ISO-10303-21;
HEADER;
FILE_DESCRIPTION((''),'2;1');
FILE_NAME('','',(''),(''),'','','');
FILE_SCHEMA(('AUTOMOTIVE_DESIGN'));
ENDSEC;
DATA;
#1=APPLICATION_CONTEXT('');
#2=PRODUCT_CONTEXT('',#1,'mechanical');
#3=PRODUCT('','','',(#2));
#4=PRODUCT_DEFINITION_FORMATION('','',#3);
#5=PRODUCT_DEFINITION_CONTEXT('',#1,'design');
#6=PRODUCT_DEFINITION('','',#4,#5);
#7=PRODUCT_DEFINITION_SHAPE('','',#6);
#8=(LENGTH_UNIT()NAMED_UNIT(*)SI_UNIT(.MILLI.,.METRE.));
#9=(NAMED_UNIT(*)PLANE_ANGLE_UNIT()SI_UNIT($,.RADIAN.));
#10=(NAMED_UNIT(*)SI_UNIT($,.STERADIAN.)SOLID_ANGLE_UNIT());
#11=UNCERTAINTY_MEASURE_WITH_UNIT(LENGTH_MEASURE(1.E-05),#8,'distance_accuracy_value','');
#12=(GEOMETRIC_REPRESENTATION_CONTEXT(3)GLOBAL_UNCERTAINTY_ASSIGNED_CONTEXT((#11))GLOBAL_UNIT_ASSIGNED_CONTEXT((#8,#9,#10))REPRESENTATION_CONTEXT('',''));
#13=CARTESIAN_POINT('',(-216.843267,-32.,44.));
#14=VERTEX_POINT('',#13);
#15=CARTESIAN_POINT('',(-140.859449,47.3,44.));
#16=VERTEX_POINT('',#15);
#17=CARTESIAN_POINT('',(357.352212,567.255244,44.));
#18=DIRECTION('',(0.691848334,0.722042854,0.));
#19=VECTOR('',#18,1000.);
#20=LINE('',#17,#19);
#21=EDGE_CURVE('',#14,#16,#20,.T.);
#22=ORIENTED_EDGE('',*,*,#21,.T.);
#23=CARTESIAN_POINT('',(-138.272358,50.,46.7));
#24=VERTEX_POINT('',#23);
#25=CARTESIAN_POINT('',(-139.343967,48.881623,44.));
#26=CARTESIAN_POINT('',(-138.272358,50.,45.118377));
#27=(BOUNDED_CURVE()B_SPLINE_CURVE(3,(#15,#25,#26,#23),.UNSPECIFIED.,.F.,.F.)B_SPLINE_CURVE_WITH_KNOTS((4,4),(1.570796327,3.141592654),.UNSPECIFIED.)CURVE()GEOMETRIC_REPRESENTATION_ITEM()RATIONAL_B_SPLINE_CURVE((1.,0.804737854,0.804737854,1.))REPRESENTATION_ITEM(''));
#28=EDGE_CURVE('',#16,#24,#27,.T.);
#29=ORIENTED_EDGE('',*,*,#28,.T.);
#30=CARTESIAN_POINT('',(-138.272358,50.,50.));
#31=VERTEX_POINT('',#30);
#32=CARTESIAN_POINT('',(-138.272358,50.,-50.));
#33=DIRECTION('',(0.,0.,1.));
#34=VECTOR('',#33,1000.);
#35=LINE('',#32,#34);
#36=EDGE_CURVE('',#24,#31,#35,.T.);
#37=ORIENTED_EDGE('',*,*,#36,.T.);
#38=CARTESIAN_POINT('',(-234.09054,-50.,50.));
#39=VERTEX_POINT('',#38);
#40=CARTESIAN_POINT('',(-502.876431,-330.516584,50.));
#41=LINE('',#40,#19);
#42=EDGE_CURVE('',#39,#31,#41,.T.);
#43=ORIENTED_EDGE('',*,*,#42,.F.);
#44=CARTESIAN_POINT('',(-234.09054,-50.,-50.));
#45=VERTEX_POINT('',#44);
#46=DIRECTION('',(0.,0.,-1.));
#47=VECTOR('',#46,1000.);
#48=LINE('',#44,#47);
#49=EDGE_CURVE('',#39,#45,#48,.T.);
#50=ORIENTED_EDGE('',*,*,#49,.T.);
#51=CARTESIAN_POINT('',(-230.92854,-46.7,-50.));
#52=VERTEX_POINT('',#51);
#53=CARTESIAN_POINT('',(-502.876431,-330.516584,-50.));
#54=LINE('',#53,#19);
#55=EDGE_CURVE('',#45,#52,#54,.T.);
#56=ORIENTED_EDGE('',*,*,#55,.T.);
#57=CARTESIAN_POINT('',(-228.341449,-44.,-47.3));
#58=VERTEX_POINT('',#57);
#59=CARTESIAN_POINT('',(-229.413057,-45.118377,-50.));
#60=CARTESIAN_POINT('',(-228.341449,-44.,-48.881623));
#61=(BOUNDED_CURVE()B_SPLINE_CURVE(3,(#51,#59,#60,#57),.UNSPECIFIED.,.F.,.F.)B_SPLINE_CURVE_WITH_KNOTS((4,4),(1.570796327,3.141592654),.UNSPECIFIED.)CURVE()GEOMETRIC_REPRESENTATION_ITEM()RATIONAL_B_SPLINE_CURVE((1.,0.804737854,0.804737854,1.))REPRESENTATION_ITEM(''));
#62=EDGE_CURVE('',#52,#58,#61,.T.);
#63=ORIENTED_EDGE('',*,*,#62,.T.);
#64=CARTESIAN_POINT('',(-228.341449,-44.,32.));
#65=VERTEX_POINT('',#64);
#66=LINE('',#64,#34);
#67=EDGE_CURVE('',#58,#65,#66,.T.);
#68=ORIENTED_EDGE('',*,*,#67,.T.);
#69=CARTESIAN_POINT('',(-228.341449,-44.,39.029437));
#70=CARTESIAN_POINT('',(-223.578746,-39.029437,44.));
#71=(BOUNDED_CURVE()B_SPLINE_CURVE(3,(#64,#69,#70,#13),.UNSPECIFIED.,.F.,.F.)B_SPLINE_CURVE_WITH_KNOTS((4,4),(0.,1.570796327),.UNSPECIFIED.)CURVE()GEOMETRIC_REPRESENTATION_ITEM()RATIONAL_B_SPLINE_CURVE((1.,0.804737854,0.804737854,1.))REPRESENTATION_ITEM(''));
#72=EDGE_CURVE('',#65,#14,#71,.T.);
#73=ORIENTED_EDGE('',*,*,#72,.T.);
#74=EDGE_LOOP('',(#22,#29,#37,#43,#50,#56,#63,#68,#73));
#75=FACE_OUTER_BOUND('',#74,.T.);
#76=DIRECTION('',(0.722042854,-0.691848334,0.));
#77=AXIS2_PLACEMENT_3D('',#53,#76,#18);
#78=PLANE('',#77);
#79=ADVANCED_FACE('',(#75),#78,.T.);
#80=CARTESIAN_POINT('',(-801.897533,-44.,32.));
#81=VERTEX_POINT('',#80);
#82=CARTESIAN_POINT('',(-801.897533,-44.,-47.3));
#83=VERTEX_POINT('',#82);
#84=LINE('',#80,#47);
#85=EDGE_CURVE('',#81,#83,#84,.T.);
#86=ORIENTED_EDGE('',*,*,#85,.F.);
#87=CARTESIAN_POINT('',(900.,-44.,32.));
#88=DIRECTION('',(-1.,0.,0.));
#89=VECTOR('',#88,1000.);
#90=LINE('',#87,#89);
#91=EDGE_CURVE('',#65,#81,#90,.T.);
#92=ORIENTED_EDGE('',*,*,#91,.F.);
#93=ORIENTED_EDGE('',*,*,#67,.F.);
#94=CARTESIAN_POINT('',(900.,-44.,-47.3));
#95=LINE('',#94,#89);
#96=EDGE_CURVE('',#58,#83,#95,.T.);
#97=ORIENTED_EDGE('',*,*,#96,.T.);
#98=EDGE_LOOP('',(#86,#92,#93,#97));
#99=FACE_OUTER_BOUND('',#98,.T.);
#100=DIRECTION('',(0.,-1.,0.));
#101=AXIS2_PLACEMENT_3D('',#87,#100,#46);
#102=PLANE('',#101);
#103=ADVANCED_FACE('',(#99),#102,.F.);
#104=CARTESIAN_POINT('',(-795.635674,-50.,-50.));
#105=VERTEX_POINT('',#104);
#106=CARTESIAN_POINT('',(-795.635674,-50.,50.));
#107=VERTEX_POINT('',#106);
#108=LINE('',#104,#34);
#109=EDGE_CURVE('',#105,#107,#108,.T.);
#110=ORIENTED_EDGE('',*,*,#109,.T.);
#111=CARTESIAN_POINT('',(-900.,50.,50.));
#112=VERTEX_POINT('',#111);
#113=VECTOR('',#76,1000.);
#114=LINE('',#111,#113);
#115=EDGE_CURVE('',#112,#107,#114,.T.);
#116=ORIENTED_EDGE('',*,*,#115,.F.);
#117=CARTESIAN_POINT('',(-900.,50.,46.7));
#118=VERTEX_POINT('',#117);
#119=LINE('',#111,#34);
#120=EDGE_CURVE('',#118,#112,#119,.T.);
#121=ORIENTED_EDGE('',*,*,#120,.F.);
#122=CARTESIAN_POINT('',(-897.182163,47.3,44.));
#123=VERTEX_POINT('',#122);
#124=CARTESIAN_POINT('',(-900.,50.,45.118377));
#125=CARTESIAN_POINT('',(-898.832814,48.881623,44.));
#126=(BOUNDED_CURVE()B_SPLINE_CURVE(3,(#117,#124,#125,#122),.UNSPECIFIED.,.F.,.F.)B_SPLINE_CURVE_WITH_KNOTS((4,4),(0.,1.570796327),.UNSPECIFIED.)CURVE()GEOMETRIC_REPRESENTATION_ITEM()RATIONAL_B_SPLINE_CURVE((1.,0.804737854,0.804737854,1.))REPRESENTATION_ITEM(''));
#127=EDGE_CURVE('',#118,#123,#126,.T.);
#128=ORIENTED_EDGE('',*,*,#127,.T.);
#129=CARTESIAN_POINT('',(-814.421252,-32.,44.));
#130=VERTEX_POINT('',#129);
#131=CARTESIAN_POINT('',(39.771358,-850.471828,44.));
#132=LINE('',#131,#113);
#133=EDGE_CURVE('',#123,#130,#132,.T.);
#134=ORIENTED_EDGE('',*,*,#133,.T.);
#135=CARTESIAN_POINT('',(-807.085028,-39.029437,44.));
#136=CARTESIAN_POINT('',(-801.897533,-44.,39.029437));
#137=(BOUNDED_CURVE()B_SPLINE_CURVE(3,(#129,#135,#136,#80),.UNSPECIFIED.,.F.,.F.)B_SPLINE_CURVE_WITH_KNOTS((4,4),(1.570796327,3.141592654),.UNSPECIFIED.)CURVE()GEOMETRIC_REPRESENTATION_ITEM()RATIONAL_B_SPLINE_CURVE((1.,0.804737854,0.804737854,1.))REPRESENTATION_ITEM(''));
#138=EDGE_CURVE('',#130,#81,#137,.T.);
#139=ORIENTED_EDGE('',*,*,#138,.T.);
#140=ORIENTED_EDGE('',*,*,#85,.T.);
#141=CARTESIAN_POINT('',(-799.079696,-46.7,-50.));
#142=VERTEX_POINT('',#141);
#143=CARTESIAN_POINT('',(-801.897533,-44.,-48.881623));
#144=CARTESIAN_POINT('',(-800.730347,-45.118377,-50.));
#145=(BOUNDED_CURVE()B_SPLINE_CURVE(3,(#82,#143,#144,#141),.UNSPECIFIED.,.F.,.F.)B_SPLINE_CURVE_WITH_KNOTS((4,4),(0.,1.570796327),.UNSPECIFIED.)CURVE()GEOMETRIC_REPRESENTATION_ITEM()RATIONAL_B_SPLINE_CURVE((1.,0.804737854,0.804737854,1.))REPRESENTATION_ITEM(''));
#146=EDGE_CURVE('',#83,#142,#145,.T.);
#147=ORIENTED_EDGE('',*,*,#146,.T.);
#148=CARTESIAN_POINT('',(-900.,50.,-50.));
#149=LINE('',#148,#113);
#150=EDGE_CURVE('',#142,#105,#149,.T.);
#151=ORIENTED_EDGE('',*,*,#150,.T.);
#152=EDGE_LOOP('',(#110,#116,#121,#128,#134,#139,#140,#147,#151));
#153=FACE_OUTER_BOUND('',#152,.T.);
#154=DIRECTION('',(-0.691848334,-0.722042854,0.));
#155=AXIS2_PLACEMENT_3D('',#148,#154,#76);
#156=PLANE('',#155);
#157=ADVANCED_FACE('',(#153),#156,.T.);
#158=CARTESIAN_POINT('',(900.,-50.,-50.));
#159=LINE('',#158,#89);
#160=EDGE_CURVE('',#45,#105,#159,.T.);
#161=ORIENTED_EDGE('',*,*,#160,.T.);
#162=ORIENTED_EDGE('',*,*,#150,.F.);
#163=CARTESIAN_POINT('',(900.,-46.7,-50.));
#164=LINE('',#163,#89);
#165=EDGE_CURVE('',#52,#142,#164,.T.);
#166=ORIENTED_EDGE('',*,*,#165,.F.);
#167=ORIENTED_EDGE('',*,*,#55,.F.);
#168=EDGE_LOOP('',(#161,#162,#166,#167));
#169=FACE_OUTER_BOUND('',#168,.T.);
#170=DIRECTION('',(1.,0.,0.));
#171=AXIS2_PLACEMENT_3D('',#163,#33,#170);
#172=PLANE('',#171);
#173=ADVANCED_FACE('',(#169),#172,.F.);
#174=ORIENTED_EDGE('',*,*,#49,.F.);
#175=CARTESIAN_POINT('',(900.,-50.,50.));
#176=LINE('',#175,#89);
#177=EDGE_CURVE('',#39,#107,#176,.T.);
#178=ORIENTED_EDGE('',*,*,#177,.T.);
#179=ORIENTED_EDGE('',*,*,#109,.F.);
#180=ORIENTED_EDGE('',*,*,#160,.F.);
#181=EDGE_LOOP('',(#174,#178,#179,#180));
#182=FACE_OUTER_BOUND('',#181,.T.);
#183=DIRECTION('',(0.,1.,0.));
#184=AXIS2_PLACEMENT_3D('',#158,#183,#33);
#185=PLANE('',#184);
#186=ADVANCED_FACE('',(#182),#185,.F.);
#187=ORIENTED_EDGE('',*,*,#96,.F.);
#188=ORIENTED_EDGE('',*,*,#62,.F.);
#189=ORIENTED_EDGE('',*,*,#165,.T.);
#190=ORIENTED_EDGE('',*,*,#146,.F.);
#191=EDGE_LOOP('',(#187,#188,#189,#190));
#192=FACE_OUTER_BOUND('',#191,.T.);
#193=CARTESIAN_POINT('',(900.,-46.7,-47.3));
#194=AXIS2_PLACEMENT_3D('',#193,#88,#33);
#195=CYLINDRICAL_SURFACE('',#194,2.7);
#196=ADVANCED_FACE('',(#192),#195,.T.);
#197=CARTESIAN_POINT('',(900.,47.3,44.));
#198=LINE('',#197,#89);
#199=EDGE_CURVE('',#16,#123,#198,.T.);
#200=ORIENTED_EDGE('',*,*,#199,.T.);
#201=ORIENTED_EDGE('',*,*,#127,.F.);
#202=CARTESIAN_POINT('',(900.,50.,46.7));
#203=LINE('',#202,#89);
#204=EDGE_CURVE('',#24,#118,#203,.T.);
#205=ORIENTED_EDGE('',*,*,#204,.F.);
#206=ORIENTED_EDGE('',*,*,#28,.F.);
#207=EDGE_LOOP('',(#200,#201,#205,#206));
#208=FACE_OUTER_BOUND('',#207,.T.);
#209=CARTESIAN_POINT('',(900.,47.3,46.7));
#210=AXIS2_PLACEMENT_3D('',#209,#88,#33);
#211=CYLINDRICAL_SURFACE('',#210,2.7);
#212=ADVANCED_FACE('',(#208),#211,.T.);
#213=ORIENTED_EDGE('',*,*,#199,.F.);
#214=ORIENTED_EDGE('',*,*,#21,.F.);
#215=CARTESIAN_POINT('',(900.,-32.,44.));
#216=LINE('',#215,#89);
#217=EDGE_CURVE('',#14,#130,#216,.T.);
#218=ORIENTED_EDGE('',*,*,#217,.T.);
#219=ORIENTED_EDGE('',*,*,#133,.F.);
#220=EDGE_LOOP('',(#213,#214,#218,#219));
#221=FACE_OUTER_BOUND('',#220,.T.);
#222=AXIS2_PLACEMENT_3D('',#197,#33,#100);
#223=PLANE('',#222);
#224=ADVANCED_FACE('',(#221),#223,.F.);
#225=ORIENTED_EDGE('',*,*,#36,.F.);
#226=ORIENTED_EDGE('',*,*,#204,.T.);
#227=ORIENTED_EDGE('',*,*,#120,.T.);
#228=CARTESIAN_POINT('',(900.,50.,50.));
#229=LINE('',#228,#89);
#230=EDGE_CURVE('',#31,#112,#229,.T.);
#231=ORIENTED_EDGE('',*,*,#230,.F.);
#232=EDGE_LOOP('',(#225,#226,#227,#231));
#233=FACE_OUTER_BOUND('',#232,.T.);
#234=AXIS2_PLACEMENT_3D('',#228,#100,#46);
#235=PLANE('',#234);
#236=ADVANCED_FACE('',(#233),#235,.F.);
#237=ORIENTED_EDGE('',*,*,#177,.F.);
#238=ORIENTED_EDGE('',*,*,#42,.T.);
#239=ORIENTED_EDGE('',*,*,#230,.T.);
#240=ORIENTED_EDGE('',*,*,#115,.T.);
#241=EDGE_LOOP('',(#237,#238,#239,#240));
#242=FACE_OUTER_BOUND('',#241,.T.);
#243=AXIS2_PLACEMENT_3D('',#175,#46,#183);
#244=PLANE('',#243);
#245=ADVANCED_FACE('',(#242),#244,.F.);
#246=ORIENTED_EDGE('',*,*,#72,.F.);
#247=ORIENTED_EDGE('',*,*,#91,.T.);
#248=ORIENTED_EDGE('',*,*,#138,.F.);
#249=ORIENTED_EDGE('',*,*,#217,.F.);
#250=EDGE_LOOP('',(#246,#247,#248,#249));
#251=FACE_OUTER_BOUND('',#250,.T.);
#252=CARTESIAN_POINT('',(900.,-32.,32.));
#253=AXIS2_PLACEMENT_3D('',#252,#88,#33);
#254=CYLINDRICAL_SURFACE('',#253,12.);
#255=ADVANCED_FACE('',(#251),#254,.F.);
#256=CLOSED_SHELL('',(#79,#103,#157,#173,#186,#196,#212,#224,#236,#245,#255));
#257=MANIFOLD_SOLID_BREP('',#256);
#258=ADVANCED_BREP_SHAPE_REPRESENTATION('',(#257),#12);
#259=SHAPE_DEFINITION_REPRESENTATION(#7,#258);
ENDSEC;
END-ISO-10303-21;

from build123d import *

# Parameters (mm, degrees)
EXTRUDE1_DEPTH    = 900
SKETCH2_OUTSIDE_W = 2163.11
SKETCH2_OUTSIDE_H = 463.11
EXTRUDE5_DEPTH    = 100


with BuildPart() as part:
    # Sketch1 → Extrude1 (new, symmetric)
    with BuildSketch(Plane(origin=(0, 0, 0), x_dir=(0, 0, -1), z_dir=(1, 0, 0))):
        with BuildLine():
            Line((-44, 47.3), (-44, -32))
            ThreePointArc((-44, -32), (-40.485281374, -40.485281374), (-32, -44))
            Line((-32, -44), (47.3, -44))
            ThreePointArc((47.3, -44), (49.209188309, -44.790811691), (50, -46.7))
            Line((50, -46.7), (50, -50))
            Line((50, -50), (-50, -50))
            Line((-50, -50), (-50, 50))
            Line((-50, 50), (-46.7, 50))
            ThreePointArc((-46.7, 50), (-44.790811691, 49.209188309), (-44, 47.3))
        make_face()
    extrude(amount=EXTRUDE1_DEPTH, both=True)

    # Sketch2 outside → Extrude5 (cut)
    with BuildSketch(Plane.XY.offset(50)):
        Rectangle(SKETCH2_OUTSIDE_W, SKETCH2_OUTSIDE_H)
        Polygon((-138.272358385, 50), (-900, 50), (-502.876430533, -330.516583835), align=None, mode=Mode.SUBTRACT)
    extrude(amount=-EXTRUDE5_DEPTH, mode=Mode.SUBTRACT)


solid = part.part
